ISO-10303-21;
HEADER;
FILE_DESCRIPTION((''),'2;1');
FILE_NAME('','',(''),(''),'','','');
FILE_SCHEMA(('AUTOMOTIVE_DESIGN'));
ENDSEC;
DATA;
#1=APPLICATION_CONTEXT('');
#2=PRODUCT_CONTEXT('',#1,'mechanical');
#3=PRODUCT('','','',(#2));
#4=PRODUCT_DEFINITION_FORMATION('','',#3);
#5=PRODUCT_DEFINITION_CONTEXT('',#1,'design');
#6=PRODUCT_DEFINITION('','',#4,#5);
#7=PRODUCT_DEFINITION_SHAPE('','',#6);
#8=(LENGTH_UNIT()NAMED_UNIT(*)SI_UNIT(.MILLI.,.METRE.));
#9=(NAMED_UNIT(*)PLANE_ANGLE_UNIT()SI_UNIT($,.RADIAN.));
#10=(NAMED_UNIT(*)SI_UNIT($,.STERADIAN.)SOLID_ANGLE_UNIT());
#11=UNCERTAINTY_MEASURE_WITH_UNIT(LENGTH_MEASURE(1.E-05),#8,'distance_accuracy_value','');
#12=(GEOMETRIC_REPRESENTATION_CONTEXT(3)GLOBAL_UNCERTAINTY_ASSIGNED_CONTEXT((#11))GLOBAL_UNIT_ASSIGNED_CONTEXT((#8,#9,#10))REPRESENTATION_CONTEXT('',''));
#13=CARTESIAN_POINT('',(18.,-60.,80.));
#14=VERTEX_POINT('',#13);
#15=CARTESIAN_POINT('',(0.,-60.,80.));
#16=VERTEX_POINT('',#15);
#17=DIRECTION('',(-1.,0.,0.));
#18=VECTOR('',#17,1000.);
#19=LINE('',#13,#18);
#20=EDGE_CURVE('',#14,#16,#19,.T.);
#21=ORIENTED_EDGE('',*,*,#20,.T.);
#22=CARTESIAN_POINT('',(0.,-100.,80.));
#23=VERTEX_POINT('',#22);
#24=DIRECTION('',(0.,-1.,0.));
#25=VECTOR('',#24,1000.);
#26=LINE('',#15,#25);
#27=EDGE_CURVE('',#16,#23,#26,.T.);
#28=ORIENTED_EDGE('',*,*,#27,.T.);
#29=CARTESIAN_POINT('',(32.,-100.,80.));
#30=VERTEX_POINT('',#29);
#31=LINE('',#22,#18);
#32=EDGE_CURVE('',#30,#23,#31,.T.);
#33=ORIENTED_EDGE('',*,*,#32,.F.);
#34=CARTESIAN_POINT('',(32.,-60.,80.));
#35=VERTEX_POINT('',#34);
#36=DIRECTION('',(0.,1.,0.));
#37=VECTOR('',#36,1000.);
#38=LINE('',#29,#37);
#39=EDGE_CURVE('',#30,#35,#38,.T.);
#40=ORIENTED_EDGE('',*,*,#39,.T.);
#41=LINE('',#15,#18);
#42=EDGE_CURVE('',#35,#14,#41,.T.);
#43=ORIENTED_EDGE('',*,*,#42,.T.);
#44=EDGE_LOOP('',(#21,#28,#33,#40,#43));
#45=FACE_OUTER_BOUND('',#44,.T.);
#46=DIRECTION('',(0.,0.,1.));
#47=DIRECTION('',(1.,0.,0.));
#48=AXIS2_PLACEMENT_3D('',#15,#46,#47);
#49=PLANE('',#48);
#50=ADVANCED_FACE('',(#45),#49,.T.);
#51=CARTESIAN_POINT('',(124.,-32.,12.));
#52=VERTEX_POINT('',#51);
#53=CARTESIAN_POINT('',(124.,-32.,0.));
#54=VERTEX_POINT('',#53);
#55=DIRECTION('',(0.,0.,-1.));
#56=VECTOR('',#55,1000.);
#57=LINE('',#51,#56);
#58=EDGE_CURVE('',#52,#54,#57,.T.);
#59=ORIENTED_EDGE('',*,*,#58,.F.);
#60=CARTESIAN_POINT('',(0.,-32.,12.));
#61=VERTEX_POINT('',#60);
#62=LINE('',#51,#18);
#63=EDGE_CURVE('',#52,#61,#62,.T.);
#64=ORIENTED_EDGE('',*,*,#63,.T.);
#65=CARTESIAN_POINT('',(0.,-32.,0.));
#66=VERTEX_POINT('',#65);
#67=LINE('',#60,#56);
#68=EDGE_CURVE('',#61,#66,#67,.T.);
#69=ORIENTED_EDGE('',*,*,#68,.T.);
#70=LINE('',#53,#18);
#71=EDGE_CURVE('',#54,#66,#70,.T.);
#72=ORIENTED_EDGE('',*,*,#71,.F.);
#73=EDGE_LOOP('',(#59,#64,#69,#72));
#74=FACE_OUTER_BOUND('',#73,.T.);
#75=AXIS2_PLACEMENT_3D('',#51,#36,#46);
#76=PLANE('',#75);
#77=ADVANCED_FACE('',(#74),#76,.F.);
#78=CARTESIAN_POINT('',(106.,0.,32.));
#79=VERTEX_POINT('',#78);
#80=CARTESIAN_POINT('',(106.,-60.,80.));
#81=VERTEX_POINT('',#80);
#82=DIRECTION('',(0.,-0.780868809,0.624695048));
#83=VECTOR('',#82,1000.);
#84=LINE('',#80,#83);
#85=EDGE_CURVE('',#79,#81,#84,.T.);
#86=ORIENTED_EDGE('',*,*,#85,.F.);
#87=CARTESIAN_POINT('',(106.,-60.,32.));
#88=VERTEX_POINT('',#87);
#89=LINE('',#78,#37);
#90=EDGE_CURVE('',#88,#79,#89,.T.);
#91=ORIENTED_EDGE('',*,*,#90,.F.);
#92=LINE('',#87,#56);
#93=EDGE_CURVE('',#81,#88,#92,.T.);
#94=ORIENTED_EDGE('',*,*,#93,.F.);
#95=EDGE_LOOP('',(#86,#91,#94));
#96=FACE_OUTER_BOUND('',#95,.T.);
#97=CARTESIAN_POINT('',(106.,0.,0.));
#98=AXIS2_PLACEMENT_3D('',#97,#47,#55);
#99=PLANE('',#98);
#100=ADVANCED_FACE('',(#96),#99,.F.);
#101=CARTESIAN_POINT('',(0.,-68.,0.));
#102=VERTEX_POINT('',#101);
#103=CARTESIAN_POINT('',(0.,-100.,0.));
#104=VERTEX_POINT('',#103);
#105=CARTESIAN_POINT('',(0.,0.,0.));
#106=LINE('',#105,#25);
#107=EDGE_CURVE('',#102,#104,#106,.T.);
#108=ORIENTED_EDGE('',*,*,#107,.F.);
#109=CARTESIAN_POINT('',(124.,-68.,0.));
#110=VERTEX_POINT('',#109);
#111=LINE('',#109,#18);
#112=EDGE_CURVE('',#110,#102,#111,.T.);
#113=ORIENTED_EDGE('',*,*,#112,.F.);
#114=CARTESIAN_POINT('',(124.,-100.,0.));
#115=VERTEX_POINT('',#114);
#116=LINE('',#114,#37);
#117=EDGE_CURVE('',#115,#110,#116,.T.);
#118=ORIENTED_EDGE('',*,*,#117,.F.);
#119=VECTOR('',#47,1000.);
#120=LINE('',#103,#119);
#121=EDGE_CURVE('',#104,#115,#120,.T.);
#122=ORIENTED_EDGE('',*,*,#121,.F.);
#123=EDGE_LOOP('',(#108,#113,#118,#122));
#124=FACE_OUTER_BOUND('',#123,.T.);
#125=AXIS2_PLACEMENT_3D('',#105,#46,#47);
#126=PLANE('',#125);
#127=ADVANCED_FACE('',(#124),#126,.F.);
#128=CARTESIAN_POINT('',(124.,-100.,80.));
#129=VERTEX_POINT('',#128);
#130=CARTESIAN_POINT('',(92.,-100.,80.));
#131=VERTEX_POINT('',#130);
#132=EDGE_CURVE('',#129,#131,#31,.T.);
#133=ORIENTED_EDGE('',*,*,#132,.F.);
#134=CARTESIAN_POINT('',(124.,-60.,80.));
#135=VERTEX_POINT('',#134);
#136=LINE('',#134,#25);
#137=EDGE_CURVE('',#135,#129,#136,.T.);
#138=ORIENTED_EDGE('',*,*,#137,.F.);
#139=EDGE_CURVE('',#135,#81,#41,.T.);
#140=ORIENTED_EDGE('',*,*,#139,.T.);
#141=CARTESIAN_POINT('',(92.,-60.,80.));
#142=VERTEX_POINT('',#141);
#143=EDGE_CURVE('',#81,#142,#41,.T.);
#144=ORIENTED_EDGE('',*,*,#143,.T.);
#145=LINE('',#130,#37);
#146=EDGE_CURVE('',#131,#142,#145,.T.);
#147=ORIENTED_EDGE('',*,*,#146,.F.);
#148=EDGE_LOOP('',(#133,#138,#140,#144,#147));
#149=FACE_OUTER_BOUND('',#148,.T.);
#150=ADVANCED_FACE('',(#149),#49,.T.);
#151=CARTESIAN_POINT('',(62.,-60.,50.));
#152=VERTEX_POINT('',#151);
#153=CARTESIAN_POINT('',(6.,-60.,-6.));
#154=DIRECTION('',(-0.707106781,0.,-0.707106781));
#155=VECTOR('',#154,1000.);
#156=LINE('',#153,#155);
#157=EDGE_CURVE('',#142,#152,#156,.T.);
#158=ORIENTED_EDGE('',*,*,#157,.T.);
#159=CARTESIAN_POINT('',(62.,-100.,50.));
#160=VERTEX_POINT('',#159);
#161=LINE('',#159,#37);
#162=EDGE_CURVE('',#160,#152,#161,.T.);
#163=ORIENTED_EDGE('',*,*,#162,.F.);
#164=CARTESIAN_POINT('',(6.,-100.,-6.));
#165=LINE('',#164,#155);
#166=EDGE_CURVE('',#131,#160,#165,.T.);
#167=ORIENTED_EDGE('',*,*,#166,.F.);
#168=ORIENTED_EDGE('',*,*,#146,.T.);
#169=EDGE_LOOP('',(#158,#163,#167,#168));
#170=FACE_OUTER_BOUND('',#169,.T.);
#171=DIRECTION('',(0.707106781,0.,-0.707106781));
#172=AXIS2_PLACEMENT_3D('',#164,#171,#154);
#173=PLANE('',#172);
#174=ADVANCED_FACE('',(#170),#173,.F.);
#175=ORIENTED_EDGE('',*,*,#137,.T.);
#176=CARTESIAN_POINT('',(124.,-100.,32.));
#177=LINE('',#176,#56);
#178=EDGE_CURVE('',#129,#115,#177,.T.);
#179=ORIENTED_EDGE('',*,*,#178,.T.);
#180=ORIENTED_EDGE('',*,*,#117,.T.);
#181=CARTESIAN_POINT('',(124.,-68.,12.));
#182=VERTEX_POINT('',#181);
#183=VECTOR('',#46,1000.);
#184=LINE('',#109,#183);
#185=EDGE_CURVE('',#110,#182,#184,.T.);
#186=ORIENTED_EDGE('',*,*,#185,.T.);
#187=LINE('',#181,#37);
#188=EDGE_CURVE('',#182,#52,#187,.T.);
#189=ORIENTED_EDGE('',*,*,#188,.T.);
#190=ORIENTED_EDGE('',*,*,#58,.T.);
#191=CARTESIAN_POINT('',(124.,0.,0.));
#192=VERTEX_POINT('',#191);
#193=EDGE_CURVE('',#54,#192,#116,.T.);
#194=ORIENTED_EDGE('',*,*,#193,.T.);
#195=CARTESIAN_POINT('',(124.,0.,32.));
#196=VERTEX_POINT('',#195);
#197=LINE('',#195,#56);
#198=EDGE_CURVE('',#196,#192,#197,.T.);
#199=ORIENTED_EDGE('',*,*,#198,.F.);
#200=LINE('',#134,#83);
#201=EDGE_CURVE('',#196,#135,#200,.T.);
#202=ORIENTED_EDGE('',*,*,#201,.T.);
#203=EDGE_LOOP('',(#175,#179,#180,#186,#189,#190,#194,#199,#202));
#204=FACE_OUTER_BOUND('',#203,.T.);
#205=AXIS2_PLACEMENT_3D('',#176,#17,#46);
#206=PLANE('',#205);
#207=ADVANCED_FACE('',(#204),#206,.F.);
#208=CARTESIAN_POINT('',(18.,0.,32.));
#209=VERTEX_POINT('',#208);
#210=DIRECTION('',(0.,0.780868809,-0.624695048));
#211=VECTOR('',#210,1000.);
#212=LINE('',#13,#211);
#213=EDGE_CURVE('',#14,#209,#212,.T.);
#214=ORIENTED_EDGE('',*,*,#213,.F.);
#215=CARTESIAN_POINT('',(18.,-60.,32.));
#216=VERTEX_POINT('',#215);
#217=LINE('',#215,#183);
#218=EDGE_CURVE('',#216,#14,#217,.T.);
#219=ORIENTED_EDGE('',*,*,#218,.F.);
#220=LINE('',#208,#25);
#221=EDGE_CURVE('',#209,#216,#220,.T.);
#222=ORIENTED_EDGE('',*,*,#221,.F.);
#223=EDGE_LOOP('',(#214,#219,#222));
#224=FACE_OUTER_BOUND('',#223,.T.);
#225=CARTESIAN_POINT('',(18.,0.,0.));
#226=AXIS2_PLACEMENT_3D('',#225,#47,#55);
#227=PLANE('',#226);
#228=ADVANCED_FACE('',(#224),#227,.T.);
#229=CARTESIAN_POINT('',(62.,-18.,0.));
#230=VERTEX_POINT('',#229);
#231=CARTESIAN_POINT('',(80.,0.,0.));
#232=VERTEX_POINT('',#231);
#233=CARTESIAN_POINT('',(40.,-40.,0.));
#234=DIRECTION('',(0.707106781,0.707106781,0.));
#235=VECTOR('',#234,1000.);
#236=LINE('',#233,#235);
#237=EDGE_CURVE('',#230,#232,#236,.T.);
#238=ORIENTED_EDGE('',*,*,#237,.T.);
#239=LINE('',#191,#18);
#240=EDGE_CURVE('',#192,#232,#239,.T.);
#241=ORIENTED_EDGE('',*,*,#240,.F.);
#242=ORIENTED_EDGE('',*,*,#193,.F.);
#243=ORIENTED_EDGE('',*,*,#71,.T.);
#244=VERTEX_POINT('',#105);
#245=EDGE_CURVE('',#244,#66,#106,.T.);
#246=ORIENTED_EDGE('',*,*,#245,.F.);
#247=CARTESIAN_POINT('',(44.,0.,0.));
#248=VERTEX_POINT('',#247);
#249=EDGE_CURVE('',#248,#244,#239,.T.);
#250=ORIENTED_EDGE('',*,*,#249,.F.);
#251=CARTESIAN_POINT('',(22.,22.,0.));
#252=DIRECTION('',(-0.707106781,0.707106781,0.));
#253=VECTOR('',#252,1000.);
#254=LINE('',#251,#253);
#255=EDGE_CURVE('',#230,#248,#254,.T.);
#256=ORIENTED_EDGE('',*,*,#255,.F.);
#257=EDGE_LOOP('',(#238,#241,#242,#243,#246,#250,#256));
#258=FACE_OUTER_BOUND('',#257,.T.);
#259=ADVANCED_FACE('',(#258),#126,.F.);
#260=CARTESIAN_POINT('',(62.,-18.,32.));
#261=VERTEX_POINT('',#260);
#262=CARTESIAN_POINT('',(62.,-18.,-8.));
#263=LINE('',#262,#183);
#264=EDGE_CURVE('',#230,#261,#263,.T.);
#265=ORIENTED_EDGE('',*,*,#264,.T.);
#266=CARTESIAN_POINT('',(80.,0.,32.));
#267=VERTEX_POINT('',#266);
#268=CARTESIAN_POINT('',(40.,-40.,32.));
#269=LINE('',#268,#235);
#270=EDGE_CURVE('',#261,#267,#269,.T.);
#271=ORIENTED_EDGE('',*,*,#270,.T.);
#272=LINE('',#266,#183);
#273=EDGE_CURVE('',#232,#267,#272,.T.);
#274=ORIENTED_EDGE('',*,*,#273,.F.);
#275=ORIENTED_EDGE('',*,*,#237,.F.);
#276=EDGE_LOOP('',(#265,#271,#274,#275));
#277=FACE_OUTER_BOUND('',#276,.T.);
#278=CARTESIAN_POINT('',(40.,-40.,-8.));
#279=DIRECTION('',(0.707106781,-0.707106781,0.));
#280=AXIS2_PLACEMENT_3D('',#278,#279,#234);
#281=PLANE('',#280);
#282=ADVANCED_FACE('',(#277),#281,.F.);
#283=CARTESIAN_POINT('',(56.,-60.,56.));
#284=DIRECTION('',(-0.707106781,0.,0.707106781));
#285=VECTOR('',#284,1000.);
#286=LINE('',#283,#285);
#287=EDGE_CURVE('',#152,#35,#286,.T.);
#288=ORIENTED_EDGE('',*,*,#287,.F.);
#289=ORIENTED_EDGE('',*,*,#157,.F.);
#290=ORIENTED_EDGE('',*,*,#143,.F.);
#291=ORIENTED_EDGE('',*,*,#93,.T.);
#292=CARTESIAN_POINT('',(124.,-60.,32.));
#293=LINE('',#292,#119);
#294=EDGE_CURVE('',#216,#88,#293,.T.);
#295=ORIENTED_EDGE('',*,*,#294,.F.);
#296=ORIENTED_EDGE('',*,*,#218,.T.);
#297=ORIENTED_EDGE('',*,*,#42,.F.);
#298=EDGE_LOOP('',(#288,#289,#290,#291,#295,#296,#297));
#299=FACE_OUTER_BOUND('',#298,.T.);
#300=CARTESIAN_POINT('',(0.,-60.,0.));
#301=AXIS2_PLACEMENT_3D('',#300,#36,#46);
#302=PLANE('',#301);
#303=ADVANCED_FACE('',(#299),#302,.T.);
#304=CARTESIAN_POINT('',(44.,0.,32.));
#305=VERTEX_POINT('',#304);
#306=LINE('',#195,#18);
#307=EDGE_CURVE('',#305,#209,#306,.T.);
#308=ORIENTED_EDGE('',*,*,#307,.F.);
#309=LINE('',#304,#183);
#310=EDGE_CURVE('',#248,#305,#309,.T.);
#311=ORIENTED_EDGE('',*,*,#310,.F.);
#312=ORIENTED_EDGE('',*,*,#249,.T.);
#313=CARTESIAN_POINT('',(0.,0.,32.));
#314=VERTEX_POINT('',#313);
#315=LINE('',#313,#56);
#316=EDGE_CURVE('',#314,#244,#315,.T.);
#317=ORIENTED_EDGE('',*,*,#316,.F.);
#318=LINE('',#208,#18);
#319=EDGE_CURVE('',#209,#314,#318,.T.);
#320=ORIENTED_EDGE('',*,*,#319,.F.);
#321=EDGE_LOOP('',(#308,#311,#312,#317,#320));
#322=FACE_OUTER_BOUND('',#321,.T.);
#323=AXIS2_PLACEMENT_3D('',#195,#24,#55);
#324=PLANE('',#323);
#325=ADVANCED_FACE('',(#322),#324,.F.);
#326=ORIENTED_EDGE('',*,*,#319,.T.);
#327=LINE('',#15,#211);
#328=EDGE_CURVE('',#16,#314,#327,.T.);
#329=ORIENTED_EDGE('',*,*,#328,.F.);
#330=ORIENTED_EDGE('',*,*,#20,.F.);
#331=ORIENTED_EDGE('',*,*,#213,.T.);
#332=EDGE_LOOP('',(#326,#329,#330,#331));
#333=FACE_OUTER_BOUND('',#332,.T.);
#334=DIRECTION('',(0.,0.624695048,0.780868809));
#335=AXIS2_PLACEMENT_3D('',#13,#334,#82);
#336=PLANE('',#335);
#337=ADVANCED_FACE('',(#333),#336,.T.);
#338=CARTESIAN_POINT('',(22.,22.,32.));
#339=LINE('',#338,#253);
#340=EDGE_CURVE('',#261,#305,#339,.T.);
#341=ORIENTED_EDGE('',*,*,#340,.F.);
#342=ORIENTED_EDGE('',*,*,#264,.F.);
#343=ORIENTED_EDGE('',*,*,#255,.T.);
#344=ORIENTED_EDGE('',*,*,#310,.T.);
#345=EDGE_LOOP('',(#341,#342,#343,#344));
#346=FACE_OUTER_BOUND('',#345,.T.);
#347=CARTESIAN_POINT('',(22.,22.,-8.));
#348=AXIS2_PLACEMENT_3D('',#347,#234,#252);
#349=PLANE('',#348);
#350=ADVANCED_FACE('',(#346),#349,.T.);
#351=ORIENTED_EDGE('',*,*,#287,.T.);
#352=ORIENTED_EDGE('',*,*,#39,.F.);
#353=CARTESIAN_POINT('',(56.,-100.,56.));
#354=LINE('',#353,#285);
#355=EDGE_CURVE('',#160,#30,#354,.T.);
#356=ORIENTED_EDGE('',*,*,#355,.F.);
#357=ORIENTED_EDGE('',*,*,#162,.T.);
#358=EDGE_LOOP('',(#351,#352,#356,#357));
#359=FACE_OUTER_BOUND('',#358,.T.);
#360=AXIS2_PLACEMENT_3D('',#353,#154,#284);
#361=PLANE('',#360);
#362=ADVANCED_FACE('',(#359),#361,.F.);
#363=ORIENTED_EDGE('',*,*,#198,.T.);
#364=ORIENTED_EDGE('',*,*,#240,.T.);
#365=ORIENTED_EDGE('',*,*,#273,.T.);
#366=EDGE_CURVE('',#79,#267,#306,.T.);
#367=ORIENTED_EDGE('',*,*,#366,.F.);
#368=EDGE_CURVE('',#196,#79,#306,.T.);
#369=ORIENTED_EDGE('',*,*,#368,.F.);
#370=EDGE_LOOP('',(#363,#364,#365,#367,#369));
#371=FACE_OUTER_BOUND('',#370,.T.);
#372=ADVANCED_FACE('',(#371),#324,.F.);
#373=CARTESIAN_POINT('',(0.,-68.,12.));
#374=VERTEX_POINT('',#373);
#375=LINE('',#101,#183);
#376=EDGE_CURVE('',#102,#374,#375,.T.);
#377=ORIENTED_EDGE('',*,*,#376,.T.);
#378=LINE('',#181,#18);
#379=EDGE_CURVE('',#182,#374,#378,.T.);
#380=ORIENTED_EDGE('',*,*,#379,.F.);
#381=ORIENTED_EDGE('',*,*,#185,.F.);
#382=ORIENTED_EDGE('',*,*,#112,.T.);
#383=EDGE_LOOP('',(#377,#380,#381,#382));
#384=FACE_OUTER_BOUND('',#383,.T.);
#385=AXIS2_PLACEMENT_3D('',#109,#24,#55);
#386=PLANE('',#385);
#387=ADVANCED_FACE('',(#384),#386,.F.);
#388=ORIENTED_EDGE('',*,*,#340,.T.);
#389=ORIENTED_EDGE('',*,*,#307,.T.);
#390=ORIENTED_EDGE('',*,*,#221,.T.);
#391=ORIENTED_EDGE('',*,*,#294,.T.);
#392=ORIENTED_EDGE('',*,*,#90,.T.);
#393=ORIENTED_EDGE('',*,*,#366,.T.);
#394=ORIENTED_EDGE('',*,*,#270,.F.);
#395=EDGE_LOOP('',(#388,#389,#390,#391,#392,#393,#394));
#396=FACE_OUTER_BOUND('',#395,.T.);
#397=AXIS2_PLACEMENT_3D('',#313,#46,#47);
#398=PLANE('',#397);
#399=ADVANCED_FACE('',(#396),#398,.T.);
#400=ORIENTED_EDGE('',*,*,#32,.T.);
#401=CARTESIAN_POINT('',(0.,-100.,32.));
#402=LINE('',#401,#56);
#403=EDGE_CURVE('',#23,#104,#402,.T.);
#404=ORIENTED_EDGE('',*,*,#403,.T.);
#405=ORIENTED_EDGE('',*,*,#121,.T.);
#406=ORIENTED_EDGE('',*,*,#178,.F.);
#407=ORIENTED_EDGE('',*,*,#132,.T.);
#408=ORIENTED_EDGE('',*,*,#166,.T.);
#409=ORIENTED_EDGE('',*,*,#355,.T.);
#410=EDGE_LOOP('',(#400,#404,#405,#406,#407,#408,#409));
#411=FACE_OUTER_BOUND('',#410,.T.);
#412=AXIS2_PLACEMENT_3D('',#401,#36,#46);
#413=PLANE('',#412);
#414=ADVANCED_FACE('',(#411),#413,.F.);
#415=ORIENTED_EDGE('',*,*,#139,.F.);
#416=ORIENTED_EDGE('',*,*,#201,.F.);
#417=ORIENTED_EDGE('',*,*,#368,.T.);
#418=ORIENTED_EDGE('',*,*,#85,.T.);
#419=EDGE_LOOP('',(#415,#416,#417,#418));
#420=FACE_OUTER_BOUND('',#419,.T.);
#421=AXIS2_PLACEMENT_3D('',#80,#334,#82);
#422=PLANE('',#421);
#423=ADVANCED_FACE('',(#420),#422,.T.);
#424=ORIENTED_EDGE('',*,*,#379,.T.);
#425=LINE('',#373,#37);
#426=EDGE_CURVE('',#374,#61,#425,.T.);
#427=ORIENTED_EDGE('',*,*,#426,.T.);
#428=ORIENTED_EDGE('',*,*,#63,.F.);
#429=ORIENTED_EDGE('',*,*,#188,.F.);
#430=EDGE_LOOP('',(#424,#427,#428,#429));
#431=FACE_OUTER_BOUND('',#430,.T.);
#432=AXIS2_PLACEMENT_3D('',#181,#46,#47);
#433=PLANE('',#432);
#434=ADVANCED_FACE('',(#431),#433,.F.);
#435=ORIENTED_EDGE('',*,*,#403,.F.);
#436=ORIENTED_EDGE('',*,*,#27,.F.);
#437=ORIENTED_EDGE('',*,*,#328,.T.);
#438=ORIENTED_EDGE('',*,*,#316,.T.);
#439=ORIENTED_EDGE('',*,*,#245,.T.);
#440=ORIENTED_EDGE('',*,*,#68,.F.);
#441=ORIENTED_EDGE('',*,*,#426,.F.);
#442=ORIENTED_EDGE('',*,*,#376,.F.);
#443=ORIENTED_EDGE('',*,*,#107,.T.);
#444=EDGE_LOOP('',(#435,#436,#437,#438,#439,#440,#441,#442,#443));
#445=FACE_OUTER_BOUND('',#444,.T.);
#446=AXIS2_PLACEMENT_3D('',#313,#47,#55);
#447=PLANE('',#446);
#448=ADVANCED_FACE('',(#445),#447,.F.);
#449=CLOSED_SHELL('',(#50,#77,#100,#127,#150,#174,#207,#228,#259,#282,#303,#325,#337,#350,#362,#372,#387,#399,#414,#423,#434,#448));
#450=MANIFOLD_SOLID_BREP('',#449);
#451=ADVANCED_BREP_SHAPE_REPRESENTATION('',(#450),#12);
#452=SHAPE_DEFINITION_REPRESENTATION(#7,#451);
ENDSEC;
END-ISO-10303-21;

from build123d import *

# Parameters (mm, degrees)
BASE_PROFILE_SKETCH_W = 124
BASE_PROFILE_SKETCH_H = 100
BASE_BLOCK_32_DEPTH   = 32
FRONT_NOTCH_SKETCH_W  = 12
FRONT_NOTCH_SKETCH_H  = 36
FRONT_NOTCH_CUT_DEPTH = 124
UPRIGHT_WALL_SKETCH_W = 124
UPRIGHT_WALL_SKETCH_H = 48
UPRIGHT_WALL_40_DEPTH = 40
WEDGE_A_18_DEPTH      = 18
WEDGE_B_18_DEPTH      = 18
V_NOTCH_CUT_DEPTH     = 40
SIDE_SLOT_CUT_DEPTH   = 40


with BuildPart() as part:
    # Base Profile Sketch → Base Block 32 (new body)
    with BuildSketch(Plane.XY):
        with Locations((62, -50)):
            Rectangle(BASE_PROFILE_SKETCH_W, BASE_PROFILE_SKETCH_H)
    extrude(amount=BASE_BLOCK_32_DEPTH)

    # Front Notch Sketch → Front Notch Cut (cut)
    with BuildSketch(Plane.ZY):
        with Locations((6, -50)):
            Rectangle(FRONT_NOTCH_SKETCH_W, FRONT_NOTCH_SKETCH_H)
    extrude(amount=-FRONT_NOTCH_CUT_DEPTH, mode=Mode.SUBTRACT)

    # Upright Wall Sketch → Upright Wall 40 (add)
    with BuildSketch(Plane.XZ.offset(100)):
        with Locations((62, 56)):
            Rectangle(UPRIGHT_WALL_SKETCH_W, UPRIGHT_WALL_SKETCH_H)
    extrude(amount=-UPRIGHT_WALL_40_DEPTH)

    # Wedge A Sketch → Wedge A 18 (add)
    with BuildSketch(Plane(origin=(124, 0, 0), x_dir=(0, 0, -1), z_dir=(1, 0, 0))):
        Polygon((-80, -60), (-32, 0), (-32, -60), align=None)
    extrude(amount=-WEDGE_A_18_DEPTH)

    # Wedge B Sketch → Wedge B 18 (add)
    with BuildSketch(Plane.ZY):
        Polygon((80, -60), (32, 0), (32, -60), align=None)
    extrude(amount=-WEDGE_B_18_DEPTH)

    # V Notch Sketch → V Notch Cut (cut)
    with BuildSketch(Plane(origin=(0, -60, 0), x_dir=(1, 0, 0), z_dir=(0, 1, 0))):
        Polygon((32, -80), (62, -80), (92, -80), (62, -50), align=None)
    extrude(amount=-V_NOTCH_CUT_DEPTH, mode=Mode.SUBTRACT)

    # Side Slot Sketch → Side Slot Cut (cut)
    with BuildSketch(Plane.XY.offset(32)):
        Polygon((80, 0), (62, 0), (44, 0), (62, -18), align=None)
    extrude(amount=-SIDE_SLOT_CUT_DEPTH, mode=Mode.SUBTRACT)


solid = part.part
